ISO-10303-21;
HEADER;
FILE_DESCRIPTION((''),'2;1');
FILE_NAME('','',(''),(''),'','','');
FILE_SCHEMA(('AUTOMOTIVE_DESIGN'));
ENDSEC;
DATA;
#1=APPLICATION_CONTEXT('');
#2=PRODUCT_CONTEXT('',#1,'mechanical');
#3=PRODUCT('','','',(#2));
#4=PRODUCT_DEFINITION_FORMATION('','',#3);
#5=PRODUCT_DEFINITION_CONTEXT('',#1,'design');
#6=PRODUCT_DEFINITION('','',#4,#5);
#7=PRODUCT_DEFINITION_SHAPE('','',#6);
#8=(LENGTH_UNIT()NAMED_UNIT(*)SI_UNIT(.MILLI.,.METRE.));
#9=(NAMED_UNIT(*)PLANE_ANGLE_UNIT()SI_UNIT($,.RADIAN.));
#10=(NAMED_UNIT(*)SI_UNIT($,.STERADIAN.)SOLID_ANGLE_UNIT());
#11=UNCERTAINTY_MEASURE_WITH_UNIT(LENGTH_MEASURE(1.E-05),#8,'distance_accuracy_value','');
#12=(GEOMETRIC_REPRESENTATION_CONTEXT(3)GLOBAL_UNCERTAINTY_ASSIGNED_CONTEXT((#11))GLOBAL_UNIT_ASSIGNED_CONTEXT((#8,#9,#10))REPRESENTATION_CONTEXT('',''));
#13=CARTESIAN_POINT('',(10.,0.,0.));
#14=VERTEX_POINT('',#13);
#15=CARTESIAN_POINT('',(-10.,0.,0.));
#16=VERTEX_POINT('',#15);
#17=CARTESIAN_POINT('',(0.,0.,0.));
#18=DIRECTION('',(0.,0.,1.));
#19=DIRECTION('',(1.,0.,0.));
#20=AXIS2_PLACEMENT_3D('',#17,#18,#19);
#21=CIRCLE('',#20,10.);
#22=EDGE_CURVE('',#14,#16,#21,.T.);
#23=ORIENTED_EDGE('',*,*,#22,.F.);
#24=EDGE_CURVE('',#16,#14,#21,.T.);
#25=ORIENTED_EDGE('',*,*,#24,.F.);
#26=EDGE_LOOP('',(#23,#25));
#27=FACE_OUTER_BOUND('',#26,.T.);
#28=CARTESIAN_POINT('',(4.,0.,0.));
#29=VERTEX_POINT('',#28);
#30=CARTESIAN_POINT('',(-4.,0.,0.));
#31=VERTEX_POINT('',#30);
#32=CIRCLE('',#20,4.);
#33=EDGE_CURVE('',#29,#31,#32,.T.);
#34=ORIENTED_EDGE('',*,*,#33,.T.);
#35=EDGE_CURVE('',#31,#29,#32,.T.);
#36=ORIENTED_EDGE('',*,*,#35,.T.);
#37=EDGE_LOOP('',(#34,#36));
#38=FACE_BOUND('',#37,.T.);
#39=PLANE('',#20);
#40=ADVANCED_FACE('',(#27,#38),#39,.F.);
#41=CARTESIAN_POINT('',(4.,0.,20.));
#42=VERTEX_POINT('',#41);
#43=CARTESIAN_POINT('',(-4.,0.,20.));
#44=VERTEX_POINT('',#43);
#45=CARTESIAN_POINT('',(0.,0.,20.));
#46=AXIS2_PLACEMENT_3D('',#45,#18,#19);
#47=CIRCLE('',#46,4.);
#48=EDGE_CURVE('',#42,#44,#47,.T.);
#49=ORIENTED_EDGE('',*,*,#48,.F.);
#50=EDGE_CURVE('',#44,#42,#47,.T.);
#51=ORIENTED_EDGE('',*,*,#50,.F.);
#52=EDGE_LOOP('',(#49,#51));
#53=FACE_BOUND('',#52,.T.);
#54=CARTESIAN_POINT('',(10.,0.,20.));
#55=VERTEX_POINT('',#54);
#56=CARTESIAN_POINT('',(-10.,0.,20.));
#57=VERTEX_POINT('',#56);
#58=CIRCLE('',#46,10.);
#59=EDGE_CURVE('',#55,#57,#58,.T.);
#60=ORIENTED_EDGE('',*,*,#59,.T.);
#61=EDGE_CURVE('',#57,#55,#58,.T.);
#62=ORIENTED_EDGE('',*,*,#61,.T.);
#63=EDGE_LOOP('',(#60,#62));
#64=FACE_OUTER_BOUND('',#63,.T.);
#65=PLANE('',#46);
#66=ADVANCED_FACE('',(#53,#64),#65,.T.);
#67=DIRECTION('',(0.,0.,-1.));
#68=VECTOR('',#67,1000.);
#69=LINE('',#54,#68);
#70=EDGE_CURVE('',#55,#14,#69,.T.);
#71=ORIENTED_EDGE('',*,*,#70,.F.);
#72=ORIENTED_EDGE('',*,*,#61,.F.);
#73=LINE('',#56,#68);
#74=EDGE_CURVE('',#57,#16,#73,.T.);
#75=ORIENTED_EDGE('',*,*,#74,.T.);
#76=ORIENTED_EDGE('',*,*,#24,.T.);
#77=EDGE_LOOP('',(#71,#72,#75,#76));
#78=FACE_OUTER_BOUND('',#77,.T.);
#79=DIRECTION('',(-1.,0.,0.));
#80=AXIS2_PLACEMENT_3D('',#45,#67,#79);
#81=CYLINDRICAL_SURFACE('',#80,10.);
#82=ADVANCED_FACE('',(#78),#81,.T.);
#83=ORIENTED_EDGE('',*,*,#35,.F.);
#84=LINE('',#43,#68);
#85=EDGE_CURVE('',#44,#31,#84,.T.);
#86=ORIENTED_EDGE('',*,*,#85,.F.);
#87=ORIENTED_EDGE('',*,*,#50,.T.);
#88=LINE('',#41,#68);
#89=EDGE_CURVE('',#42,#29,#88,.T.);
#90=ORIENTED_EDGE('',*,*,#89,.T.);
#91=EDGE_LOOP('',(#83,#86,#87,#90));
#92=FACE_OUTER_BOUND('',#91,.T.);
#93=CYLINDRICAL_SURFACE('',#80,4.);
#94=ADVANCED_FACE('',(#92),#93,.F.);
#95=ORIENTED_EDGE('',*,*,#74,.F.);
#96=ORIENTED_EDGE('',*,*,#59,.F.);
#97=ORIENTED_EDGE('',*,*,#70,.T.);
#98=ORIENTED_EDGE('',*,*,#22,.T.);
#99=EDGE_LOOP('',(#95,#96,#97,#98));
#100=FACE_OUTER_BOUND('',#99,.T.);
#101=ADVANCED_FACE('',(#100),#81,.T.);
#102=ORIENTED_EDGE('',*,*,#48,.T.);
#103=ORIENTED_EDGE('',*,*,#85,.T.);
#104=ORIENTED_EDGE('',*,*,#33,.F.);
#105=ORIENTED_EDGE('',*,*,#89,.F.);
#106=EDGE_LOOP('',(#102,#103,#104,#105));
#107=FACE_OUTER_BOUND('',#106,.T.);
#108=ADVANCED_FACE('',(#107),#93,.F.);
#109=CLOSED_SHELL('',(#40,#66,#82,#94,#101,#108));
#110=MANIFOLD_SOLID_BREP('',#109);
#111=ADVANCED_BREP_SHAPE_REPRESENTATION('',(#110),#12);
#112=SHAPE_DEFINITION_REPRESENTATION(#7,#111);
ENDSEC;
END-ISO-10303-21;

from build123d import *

# Parameters (mm, degrees)
SKETCH_1_R      = 10
SKETCH_1_R_2    = 4
EXTRUDE_1_DEPTH = 20


with BuildPart() as part:
    # 草图1 → 凸台-拉伸1 (new body)
    with BuildSketch(Plane.XY):
        Circle(SKETCH_1_R)
        Circle(SKETCH_1_R_2, mode=Mode.SUBTRACT)
    extrude(amount=EXTRUDE_1_DEPTH)


solid = part.part
